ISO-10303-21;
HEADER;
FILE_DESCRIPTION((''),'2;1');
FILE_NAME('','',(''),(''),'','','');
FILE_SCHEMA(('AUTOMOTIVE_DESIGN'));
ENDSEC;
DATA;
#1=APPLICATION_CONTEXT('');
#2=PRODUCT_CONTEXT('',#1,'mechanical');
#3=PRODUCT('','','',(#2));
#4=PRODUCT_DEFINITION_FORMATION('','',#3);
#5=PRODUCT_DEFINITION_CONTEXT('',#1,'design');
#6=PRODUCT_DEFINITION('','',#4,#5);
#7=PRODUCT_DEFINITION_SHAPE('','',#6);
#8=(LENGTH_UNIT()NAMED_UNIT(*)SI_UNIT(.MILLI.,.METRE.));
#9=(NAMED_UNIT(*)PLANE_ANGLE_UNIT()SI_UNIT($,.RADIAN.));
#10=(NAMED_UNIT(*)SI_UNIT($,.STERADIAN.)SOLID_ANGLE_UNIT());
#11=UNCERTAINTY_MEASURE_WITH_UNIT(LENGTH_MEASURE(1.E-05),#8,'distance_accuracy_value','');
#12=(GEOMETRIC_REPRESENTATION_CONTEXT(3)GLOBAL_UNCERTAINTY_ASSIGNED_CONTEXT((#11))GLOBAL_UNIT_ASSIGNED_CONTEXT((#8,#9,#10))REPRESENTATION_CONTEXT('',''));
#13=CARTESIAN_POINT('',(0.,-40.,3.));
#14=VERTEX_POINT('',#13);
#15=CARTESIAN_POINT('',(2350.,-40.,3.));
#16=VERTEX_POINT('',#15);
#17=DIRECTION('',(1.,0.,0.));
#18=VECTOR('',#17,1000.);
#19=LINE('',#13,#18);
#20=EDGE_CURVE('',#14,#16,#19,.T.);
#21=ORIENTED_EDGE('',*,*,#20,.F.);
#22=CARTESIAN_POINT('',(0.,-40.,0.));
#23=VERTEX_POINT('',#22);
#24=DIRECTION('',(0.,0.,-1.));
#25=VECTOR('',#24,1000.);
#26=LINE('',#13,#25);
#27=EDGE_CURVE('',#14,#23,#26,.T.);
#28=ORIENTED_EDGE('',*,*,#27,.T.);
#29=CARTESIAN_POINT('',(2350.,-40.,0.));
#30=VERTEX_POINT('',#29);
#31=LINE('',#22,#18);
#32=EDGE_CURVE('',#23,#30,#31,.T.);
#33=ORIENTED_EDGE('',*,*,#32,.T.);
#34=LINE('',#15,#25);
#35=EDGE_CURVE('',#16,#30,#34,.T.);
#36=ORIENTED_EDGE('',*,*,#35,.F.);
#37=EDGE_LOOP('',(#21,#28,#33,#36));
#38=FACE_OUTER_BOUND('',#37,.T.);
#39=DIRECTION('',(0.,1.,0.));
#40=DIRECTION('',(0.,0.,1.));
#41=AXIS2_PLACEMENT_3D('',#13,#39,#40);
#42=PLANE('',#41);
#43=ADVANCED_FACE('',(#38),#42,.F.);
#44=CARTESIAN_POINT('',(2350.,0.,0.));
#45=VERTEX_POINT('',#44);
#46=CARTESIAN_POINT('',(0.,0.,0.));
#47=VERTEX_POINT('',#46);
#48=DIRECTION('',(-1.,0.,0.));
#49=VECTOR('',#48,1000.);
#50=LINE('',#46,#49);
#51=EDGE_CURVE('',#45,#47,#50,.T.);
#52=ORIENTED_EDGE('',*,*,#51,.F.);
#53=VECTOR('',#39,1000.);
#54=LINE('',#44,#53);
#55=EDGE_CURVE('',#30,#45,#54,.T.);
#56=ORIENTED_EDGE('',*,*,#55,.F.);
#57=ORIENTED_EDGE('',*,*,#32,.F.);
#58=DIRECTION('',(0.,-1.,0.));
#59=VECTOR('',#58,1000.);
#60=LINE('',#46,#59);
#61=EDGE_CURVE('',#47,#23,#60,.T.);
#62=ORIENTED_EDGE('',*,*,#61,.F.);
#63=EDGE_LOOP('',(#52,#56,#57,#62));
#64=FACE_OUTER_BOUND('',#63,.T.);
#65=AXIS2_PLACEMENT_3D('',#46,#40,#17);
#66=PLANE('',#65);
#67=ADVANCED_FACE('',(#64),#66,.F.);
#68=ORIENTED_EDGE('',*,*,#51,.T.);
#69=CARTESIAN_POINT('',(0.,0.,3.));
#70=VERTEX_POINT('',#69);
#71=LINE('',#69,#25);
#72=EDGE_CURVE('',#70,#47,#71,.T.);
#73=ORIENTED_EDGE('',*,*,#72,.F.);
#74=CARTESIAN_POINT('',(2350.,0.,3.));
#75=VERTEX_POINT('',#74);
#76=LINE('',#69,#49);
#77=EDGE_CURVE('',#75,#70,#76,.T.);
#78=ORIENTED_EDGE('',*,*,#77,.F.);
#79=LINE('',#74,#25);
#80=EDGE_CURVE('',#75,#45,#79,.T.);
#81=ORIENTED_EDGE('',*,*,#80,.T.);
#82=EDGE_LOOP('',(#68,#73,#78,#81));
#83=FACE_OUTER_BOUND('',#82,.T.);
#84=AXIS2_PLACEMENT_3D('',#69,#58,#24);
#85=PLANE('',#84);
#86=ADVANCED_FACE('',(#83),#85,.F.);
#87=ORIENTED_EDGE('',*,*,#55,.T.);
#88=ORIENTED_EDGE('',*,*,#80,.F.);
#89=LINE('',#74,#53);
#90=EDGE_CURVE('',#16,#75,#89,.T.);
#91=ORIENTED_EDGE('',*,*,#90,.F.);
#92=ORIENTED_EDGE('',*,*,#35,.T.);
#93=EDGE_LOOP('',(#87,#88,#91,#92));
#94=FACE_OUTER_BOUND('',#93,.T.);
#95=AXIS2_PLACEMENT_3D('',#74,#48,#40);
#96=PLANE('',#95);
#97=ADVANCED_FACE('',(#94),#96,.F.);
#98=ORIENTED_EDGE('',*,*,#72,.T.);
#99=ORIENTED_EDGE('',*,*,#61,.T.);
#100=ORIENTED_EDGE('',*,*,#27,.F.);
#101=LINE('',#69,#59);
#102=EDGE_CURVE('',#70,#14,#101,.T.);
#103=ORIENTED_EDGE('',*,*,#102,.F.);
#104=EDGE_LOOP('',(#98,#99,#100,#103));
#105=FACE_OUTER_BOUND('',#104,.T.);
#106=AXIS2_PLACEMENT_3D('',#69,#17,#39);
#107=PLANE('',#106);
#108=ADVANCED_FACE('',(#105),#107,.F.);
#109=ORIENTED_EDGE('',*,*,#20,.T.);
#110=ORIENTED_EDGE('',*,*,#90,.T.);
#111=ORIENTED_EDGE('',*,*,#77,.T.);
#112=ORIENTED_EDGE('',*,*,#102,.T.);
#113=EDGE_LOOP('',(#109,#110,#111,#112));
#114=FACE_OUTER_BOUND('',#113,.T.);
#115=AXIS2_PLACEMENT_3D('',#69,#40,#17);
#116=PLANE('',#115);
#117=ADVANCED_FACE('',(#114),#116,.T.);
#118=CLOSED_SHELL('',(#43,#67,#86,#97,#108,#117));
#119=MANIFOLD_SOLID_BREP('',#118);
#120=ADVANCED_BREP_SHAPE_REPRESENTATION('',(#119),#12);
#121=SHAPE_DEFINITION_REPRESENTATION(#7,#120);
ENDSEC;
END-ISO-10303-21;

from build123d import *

# Parameters (mm, degrees)
SKETCH1_W           = 2350
SKETCH1_H           = 40
BOSS_EXTRUDE1_DEPTH = 3


with BuildPart() as part:
    # Sketch1 → Boss-Extrude1 (new body)
    with BuildSketch(Plane.XY):
        with Locations((1175, -20)):
            Rectangle(SKETCH1_W, SKETCH1_H)
    extrude(amount=BOSS_EXTRUDE1_DEPTH)


solid = part.part
